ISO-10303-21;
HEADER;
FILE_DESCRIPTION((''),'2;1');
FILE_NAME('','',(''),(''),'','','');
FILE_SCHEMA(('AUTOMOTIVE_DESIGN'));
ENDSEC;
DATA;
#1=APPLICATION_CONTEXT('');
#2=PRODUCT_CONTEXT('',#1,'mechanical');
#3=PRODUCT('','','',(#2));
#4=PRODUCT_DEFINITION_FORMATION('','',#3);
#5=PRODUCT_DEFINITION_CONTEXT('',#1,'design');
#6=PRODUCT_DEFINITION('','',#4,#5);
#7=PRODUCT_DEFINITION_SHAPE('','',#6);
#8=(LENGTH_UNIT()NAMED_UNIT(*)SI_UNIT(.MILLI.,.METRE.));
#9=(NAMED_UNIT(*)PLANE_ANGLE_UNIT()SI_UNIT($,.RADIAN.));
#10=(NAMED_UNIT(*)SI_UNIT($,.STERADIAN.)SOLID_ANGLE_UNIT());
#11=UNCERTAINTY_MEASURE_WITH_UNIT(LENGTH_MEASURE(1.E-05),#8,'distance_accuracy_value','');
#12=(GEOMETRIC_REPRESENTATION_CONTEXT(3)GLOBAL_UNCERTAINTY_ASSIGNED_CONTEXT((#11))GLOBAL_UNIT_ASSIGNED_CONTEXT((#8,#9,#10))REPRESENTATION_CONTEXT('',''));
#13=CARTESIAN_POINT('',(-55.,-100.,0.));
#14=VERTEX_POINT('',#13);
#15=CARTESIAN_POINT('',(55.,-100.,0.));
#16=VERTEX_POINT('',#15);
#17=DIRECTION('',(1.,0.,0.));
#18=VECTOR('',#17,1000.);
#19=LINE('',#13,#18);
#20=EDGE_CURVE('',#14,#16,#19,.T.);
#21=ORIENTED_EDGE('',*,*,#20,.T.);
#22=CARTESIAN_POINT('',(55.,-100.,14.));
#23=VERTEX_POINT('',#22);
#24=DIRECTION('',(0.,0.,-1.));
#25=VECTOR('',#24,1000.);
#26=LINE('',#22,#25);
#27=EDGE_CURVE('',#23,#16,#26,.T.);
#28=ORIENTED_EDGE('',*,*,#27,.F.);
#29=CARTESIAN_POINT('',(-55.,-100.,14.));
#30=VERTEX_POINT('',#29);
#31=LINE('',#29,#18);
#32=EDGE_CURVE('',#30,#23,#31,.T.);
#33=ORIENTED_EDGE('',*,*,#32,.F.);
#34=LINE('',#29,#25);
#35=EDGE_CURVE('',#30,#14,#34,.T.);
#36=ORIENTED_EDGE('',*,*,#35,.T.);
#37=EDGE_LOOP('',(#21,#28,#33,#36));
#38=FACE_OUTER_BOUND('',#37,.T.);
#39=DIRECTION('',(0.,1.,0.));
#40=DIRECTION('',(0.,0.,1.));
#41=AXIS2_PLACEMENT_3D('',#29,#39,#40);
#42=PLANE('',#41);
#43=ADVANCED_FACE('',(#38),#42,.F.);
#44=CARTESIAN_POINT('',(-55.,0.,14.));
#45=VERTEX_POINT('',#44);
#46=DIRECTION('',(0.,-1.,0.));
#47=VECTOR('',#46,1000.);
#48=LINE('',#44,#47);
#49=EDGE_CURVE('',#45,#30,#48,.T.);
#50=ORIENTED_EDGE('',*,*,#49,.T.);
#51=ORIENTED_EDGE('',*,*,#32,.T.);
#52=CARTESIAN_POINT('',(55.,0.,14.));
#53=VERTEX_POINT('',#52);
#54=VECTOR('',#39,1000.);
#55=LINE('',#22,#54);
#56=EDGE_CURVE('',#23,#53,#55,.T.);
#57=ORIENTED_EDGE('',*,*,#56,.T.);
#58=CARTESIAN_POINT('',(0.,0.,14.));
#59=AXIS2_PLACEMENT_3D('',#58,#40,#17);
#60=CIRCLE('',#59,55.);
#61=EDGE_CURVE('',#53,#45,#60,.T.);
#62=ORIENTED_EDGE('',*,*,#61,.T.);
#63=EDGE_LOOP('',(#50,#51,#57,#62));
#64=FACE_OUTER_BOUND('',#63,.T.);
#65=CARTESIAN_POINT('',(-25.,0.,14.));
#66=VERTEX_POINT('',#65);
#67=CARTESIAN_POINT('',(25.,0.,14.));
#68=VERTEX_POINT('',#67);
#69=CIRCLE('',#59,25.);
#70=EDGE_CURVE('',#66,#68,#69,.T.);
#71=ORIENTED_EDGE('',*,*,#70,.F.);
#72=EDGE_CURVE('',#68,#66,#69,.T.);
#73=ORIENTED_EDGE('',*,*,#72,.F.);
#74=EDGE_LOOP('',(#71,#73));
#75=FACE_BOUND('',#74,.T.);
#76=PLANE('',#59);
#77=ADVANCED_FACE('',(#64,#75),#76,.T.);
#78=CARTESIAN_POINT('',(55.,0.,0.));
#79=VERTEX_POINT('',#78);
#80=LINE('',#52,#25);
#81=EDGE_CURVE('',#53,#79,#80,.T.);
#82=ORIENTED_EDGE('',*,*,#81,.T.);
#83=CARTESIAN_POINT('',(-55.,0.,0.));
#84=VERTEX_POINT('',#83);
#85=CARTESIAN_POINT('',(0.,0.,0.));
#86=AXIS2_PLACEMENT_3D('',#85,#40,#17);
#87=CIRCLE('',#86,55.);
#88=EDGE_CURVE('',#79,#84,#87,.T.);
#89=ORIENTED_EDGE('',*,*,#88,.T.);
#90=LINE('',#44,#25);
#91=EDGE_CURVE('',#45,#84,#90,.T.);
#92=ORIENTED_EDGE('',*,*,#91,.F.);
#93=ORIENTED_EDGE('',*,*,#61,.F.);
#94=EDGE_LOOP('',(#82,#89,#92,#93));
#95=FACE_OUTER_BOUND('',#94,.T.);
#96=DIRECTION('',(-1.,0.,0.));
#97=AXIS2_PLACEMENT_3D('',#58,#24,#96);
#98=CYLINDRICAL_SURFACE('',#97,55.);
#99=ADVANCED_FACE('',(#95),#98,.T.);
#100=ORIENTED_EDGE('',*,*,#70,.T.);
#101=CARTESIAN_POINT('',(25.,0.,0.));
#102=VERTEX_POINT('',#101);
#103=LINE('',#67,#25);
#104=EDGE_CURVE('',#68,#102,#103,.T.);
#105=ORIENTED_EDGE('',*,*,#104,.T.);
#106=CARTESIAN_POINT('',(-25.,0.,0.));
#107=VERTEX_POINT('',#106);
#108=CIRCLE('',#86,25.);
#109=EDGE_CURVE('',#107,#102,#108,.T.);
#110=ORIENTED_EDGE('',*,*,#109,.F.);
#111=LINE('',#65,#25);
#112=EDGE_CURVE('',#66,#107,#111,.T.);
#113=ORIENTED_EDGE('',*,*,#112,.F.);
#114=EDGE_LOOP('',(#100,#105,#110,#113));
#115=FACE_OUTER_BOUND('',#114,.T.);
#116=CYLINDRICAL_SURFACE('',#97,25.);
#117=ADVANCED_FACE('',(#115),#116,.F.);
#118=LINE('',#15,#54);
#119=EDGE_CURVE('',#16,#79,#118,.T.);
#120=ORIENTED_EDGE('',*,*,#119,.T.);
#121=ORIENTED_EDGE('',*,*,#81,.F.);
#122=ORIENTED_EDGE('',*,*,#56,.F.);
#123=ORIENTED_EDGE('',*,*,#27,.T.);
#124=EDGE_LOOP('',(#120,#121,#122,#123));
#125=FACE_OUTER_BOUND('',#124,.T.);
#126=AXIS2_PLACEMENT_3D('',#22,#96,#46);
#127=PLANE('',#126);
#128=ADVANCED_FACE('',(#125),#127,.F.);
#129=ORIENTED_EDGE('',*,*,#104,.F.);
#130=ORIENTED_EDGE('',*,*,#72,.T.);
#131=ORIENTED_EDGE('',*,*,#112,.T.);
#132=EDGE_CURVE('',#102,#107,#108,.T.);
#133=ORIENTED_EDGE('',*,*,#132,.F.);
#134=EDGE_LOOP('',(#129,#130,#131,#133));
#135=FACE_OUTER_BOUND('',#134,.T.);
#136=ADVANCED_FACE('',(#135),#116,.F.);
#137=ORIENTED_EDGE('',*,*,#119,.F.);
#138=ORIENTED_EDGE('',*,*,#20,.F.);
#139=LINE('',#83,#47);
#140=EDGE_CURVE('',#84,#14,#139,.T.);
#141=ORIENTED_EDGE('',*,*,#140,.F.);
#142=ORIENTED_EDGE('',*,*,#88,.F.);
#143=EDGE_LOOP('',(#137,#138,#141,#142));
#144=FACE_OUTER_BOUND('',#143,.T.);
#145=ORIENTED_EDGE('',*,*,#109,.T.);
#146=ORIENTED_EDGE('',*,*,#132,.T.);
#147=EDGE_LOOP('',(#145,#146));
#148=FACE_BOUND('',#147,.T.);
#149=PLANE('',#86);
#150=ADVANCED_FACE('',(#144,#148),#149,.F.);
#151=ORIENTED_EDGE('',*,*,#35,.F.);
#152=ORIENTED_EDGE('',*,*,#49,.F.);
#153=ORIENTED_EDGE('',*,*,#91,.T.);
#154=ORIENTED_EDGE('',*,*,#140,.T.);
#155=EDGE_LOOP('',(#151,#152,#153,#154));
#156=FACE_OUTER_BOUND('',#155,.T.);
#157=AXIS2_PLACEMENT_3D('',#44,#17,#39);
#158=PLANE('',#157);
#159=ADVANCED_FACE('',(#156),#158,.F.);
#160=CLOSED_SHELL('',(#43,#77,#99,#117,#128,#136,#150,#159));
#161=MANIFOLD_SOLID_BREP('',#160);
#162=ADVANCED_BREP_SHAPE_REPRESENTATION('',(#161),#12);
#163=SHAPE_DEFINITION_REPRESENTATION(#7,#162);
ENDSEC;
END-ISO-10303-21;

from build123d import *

# Parameters (mm, degrees)
SKETCH1_R           = 25
BOSS_EXTRUDE1_DEPTH = 14


with BuildPart() as part:
    # Sketch1 → Boss-Extrude1 (new body)
    with BuildSketch(Plane.XY):
        with BuildLine():
            Line((-55, 0), (-55, -100))
            Line((-55, -100), (55, -100))
            Line((55, -100), (55, 0))
            ThreePointArc((55, 0), (0, 55), (-55, 0))
        make_face()
        Circle(SKETCH1_R, mode=Mode.SUBTRACT)
    extrude(amount=BOSS_EXTRUDE1_DEPTH)


solid = part.part
